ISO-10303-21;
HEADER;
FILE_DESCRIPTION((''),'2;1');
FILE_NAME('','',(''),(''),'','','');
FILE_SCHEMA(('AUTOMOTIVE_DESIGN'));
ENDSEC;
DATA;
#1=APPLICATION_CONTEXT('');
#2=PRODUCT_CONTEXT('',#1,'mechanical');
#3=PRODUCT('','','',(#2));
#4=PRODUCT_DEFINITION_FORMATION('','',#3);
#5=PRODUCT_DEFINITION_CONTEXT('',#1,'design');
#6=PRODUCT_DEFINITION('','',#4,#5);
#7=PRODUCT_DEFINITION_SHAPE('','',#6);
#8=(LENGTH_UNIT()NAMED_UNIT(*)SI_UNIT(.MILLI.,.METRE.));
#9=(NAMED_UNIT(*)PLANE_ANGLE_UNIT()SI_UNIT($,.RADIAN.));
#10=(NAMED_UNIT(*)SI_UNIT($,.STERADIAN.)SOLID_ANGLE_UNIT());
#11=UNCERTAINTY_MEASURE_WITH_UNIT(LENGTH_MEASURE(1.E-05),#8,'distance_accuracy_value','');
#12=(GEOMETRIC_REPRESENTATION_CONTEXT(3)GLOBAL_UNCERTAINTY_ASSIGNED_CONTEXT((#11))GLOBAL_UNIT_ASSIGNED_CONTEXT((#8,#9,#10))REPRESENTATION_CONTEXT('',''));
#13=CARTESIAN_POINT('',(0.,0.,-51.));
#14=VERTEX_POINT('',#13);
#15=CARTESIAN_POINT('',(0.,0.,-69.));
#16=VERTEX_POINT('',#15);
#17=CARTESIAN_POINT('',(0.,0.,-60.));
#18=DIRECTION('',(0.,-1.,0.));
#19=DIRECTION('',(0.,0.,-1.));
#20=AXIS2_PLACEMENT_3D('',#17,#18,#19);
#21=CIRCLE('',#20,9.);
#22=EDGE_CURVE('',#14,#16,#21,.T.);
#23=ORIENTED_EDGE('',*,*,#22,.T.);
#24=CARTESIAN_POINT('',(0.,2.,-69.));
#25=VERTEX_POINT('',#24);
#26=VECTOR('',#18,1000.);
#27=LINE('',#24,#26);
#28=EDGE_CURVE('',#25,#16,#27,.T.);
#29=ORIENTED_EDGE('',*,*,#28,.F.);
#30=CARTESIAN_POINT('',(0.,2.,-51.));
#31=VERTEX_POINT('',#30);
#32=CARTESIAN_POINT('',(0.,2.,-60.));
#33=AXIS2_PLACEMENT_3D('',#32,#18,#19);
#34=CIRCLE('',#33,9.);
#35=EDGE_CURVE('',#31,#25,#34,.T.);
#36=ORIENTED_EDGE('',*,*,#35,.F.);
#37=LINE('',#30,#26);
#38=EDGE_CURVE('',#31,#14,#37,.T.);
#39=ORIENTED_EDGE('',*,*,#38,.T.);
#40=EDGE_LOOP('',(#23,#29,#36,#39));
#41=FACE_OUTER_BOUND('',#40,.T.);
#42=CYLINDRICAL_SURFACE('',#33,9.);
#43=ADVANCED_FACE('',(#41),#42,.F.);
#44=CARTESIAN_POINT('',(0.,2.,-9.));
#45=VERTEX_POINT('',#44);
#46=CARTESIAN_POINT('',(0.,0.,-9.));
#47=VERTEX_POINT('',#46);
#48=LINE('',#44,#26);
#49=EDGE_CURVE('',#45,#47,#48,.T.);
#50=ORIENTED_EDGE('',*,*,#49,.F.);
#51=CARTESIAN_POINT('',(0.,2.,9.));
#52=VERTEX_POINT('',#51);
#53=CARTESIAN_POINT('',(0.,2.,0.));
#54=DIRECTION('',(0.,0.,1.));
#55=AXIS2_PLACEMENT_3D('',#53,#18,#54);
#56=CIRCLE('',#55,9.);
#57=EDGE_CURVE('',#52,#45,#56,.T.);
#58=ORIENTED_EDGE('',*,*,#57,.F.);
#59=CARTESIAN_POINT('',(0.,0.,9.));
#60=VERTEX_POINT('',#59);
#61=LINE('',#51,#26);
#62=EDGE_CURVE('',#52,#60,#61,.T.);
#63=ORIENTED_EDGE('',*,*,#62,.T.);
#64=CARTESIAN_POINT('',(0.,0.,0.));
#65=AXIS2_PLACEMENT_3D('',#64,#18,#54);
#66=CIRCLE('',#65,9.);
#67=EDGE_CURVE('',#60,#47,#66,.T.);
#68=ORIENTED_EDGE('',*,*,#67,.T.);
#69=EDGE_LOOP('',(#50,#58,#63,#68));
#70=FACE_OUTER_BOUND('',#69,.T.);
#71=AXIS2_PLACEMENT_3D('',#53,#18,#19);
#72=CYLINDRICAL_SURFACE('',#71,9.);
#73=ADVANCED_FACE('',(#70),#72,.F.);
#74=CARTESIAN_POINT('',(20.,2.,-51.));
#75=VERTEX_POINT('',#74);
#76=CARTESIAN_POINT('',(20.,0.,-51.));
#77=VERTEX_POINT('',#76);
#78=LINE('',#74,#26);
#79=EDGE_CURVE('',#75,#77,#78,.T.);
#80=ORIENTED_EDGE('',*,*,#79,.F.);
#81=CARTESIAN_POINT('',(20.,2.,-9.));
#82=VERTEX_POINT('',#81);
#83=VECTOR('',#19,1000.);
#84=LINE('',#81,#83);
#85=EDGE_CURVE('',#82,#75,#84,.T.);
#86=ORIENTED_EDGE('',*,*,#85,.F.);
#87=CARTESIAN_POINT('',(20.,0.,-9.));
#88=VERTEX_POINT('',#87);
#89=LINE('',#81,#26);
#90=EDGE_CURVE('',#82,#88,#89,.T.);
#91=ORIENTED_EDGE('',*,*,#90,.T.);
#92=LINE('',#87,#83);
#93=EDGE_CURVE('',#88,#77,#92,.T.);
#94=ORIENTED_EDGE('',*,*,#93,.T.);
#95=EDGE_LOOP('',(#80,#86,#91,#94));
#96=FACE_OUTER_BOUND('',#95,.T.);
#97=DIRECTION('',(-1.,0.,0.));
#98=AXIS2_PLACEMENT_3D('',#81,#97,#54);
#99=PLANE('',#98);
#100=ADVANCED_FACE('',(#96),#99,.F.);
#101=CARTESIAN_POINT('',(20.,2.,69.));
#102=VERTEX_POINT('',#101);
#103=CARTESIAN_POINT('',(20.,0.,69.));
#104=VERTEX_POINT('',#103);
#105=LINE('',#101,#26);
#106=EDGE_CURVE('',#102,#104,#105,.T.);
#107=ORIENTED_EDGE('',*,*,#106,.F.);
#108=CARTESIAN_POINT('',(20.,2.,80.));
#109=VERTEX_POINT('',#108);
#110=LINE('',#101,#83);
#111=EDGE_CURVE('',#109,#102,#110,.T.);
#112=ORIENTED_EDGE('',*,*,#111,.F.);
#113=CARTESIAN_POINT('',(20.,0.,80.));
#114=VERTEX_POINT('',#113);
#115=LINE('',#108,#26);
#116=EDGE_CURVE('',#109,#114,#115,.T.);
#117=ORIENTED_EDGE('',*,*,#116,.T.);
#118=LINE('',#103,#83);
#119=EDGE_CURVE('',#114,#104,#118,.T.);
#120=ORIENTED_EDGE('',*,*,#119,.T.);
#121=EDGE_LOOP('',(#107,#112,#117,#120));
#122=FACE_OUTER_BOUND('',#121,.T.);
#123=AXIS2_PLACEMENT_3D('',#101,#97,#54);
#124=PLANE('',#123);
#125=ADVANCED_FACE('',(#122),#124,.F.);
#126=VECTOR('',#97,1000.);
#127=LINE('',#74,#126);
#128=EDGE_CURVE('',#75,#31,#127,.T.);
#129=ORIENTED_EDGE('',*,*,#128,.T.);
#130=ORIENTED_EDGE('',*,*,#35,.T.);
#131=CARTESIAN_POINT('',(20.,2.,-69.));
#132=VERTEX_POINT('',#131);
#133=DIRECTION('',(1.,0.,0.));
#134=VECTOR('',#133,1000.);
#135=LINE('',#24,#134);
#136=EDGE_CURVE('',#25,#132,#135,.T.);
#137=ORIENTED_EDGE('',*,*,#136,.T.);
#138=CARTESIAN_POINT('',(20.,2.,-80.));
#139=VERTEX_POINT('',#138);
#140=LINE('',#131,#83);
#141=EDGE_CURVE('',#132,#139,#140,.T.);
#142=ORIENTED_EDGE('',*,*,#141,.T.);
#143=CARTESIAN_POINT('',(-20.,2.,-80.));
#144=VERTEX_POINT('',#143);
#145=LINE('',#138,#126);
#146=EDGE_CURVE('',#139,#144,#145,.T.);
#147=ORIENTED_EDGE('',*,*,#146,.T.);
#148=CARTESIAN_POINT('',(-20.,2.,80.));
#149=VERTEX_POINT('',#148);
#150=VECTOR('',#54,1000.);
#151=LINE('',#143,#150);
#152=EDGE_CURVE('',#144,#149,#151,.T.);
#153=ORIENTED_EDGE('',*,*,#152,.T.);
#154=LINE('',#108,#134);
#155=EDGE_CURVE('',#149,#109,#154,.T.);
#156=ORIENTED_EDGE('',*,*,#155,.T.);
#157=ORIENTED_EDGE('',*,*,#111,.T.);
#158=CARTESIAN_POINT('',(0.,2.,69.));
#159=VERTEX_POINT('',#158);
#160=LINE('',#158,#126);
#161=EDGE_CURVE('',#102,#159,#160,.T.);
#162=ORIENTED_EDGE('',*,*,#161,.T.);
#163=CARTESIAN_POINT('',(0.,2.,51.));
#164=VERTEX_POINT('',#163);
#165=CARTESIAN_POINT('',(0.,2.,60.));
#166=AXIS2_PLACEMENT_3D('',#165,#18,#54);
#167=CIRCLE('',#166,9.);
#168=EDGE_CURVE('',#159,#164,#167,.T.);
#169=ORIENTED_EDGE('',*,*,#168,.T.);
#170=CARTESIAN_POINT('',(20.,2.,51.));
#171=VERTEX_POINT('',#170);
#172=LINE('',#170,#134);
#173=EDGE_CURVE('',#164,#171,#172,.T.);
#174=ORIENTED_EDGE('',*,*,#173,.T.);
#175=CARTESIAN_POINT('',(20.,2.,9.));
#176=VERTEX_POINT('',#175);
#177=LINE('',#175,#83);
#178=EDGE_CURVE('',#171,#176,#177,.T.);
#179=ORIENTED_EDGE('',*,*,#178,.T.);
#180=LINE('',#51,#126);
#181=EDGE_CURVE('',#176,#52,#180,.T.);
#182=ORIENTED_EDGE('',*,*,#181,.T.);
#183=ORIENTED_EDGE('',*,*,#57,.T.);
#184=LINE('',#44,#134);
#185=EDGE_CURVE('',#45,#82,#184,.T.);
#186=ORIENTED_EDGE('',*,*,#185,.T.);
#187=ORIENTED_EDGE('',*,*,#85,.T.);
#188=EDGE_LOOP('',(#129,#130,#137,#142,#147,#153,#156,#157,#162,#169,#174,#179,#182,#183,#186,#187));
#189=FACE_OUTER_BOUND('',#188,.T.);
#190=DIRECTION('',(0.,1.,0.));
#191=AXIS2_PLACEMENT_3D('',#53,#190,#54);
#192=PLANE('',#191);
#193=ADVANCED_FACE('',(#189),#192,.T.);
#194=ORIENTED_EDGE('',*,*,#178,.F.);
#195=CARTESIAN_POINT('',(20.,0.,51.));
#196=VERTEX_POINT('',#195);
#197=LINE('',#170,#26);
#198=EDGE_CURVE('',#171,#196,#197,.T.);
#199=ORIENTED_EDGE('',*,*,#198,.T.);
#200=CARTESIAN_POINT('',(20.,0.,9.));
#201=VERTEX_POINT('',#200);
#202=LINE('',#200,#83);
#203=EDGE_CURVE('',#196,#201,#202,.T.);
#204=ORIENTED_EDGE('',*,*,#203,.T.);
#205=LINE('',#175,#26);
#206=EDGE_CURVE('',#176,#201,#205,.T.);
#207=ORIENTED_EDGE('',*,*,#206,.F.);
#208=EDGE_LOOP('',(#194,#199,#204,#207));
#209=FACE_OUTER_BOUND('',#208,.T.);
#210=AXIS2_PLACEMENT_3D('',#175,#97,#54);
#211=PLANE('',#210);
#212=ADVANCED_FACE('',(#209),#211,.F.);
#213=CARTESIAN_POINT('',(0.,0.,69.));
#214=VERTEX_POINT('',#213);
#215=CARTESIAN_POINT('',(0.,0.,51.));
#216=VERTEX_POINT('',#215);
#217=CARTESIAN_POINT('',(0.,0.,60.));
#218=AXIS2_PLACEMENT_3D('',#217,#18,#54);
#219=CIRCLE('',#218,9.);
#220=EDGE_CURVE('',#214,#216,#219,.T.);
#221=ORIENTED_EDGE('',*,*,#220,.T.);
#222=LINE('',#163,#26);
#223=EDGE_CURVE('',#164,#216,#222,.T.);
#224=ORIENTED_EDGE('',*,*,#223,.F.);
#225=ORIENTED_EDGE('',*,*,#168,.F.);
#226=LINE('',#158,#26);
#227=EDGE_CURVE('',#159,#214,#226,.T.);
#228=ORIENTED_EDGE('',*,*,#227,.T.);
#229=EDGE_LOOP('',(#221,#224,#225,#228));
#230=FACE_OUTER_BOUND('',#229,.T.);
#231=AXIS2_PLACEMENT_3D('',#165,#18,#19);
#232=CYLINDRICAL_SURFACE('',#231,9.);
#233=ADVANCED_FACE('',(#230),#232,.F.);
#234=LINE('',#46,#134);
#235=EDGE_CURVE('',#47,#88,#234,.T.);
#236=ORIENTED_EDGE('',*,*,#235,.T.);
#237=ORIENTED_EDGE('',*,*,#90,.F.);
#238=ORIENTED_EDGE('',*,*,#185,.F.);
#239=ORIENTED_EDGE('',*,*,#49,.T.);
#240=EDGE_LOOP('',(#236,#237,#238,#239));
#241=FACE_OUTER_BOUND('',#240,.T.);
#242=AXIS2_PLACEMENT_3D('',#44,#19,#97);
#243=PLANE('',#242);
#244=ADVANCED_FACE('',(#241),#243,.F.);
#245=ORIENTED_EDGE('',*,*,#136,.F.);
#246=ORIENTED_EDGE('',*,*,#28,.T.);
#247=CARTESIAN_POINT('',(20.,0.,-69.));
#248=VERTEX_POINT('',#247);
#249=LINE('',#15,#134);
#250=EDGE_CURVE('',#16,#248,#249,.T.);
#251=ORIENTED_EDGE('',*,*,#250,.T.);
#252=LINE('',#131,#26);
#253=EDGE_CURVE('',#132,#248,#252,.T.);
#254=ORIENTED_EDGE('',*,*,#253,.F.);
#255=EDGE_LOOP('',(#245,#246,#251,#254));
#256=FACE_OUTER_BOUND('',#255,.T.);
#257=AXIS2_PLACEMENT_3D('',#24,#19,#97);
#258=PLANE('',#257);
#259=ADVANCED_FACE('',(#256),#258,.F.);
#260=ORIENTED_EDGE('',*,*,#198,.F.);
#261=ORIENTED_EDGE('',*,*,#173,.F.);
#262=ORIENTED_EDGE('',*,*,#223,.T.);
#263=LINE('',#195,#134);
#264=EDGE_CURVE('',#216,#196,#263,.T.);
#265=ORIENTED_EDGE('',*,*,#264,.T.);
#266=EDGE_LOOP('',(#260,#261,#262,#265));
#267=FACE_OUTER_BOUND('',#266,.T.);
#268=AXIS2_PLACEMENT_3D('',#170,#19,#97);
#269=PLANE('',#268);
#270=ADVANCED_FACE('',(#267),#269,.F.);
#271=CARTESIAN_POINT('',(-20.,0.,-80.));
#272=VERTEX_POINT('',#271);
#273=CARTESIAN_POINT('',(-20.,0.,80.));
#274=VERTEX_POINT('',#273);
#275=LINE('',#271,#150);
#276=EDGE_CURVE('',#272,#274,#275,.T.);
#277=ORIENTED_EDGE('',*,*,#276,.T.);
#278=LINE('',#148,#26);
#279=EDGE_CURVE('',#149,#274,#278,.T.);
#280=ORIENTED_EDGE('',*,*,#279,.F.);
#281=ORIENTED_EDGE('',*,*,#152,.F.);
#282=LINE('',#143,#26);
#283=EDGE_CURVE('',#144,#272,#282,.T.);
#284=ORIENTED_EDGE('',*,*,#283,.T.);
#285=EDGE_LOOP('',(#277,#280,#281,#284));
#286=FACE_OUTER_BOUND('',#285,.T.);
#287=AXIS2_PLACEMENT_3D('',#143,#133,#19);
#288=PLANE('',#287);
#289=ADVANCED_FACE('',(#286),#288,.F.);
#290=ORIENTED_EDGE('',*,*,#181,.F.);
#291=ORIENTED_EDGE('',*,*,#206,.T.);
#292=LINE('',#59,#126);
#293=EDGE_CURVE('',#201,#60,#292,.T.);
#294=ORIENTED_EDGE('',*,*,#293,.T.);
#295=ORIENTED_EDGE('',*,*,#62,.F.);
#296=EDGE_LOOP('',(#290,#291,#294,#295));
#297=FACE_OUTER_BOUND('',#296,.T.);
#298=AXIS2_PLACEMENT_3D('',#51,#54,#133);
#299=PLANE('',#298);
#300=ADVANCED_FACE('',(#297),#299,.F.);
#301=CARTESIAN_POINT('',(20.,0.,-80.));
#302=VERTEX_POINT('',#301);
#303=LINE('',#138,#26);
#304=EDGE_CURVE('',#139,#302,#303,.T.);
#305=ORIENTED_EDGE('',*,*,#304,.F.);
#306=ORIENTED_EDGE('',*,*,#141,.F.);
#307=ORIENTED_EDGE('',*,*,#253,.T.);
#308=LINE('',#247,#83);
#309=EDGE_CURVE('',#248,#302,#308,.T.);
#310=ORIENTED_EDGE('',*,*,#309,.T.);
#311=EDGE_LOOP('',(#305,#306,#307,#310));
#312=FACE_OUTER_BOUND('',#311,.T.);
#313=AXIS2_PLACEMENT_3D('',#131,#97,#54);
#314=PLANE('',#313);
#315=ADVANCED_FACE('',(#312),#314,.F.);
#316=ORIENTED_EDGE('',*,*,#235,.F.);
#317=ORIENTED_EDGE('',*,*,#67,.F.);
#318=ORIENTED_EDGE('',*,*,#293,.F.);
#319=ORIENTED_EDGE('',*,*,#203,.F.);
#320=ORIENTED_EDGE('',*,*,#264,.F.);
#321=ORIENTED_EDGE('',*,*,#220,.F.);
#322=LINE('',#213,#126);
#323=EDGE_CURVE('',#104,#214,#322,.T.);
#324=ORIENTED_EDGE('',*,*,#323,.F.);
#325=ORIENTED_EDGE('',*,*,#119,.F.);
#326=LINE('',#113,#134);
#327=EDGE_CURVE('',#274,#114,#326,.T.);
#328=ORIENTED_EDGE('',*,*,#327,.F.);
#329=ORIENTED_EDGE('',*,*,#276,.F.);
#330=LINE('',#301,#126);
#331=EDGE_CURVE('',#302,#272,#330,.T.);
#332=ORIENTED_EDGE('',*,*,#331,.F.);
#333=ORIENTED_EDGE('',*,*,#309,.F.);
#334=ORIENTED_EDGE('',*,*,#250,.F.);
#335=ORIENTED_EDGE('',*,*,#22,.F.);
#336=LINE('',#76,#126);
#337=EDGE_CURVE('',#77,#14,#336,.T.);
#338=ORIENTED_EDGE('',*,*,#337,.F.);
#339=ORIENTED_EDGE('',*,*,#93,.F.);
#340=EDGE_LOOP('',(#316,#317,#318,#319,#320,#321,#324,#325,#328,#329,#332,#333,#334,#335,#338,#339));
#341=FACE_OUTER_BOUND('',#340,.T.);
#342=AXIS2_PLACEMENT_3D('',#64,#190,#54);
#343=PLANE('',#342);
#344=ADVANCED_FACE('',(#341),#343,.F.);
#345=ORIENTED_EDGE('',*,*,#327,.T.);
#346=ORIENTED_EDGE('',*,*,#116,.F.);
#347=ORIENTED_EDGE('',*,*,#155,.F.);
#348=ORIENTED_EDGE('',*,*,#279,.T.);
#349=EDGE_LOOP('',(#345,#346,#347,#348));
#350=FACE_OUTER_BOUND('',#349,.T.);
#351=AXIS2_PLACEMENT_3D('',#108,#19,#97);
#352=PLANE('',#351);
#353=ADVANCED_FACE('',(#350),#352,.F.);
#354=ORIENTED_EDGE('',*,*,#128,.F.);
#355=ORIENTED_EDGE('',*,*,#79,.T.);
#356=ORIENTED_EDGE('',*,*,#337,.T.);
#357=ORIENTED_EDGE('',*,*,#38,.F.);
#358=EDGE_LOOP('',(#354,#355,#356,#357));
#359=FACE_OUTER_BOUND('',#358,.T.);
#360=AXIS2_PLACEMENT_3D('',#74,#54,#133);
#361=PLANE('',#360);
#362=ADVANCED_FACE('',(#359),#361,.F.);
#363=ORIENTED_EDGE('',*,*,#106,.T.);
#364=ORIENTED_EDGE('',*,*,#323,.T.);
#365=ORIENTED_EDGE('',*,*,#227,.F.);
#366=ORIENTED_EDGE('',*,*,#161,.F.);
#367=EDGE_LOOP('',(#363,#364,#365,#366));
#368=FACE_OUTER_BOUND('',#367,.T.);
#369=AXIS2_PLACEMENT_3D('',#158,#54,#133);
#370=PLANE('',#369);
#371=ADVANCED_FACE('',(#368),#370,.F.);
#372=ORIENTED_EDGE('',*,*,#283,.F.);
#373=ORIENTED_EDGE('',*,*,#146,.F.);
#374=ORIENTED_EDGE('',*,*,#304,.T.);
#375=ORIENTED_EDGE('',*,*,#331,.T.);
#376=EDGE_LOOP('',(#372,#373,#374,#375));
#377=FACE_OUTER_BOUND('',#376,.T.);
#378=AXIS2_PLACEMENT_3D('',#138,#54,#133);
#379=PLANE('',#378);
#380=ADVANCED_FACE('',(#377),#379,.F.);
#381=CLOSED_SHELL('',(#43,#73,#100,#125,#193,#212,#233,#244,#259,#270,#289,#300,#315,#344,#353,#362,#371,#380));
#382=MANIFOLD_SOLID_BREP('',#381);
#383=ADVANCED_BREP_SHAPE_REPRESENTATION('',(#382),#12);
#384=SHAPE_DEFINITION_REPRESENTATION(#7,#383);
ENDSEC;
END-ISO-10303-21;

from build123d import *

# Parameters (mm, degrees)
EXTRUDE_1_DEPTH = 2


with BuildPart() as part:
    # 草图1 → 凸台-拉伸1 (new body)
    with BuildSketch(Plane(origin=(0, 0, 0), x_dir=(1, 0, 0), z_dir=(0, 1, 0))):
        with BuildLine():
            Line((0, 9), (20, 9))
            Line((20, 9), (20, 51))
            Line((20, 51), (0, 51))
            ThreePointArc((0, 51), (-9, 60), (0, 69))
            Line((0, 69), (20, 69))
            Line((20, 69), (20, 80))
            Line((20, 80), (-20, 80))
            Line((-20, 80), (-20, -80))
            Line((-20, -80), (20, -80))
            Line((20, -80), (20, -69))
            Line((20, -69), (0, -69))
            ThreePointArc((0, -69), (-9, -60), (0, -51))
            Line((0, -51), (20, -51))
            Line((20, -51), (20, -9))
            Line((20, -9), (0, -9))
            ThreePointArc((0, -9), (-9, 0), (0, 9))
        make_face()
    extrude(amount=EXTRUDE_1_DEPTH)


solid = part.part
